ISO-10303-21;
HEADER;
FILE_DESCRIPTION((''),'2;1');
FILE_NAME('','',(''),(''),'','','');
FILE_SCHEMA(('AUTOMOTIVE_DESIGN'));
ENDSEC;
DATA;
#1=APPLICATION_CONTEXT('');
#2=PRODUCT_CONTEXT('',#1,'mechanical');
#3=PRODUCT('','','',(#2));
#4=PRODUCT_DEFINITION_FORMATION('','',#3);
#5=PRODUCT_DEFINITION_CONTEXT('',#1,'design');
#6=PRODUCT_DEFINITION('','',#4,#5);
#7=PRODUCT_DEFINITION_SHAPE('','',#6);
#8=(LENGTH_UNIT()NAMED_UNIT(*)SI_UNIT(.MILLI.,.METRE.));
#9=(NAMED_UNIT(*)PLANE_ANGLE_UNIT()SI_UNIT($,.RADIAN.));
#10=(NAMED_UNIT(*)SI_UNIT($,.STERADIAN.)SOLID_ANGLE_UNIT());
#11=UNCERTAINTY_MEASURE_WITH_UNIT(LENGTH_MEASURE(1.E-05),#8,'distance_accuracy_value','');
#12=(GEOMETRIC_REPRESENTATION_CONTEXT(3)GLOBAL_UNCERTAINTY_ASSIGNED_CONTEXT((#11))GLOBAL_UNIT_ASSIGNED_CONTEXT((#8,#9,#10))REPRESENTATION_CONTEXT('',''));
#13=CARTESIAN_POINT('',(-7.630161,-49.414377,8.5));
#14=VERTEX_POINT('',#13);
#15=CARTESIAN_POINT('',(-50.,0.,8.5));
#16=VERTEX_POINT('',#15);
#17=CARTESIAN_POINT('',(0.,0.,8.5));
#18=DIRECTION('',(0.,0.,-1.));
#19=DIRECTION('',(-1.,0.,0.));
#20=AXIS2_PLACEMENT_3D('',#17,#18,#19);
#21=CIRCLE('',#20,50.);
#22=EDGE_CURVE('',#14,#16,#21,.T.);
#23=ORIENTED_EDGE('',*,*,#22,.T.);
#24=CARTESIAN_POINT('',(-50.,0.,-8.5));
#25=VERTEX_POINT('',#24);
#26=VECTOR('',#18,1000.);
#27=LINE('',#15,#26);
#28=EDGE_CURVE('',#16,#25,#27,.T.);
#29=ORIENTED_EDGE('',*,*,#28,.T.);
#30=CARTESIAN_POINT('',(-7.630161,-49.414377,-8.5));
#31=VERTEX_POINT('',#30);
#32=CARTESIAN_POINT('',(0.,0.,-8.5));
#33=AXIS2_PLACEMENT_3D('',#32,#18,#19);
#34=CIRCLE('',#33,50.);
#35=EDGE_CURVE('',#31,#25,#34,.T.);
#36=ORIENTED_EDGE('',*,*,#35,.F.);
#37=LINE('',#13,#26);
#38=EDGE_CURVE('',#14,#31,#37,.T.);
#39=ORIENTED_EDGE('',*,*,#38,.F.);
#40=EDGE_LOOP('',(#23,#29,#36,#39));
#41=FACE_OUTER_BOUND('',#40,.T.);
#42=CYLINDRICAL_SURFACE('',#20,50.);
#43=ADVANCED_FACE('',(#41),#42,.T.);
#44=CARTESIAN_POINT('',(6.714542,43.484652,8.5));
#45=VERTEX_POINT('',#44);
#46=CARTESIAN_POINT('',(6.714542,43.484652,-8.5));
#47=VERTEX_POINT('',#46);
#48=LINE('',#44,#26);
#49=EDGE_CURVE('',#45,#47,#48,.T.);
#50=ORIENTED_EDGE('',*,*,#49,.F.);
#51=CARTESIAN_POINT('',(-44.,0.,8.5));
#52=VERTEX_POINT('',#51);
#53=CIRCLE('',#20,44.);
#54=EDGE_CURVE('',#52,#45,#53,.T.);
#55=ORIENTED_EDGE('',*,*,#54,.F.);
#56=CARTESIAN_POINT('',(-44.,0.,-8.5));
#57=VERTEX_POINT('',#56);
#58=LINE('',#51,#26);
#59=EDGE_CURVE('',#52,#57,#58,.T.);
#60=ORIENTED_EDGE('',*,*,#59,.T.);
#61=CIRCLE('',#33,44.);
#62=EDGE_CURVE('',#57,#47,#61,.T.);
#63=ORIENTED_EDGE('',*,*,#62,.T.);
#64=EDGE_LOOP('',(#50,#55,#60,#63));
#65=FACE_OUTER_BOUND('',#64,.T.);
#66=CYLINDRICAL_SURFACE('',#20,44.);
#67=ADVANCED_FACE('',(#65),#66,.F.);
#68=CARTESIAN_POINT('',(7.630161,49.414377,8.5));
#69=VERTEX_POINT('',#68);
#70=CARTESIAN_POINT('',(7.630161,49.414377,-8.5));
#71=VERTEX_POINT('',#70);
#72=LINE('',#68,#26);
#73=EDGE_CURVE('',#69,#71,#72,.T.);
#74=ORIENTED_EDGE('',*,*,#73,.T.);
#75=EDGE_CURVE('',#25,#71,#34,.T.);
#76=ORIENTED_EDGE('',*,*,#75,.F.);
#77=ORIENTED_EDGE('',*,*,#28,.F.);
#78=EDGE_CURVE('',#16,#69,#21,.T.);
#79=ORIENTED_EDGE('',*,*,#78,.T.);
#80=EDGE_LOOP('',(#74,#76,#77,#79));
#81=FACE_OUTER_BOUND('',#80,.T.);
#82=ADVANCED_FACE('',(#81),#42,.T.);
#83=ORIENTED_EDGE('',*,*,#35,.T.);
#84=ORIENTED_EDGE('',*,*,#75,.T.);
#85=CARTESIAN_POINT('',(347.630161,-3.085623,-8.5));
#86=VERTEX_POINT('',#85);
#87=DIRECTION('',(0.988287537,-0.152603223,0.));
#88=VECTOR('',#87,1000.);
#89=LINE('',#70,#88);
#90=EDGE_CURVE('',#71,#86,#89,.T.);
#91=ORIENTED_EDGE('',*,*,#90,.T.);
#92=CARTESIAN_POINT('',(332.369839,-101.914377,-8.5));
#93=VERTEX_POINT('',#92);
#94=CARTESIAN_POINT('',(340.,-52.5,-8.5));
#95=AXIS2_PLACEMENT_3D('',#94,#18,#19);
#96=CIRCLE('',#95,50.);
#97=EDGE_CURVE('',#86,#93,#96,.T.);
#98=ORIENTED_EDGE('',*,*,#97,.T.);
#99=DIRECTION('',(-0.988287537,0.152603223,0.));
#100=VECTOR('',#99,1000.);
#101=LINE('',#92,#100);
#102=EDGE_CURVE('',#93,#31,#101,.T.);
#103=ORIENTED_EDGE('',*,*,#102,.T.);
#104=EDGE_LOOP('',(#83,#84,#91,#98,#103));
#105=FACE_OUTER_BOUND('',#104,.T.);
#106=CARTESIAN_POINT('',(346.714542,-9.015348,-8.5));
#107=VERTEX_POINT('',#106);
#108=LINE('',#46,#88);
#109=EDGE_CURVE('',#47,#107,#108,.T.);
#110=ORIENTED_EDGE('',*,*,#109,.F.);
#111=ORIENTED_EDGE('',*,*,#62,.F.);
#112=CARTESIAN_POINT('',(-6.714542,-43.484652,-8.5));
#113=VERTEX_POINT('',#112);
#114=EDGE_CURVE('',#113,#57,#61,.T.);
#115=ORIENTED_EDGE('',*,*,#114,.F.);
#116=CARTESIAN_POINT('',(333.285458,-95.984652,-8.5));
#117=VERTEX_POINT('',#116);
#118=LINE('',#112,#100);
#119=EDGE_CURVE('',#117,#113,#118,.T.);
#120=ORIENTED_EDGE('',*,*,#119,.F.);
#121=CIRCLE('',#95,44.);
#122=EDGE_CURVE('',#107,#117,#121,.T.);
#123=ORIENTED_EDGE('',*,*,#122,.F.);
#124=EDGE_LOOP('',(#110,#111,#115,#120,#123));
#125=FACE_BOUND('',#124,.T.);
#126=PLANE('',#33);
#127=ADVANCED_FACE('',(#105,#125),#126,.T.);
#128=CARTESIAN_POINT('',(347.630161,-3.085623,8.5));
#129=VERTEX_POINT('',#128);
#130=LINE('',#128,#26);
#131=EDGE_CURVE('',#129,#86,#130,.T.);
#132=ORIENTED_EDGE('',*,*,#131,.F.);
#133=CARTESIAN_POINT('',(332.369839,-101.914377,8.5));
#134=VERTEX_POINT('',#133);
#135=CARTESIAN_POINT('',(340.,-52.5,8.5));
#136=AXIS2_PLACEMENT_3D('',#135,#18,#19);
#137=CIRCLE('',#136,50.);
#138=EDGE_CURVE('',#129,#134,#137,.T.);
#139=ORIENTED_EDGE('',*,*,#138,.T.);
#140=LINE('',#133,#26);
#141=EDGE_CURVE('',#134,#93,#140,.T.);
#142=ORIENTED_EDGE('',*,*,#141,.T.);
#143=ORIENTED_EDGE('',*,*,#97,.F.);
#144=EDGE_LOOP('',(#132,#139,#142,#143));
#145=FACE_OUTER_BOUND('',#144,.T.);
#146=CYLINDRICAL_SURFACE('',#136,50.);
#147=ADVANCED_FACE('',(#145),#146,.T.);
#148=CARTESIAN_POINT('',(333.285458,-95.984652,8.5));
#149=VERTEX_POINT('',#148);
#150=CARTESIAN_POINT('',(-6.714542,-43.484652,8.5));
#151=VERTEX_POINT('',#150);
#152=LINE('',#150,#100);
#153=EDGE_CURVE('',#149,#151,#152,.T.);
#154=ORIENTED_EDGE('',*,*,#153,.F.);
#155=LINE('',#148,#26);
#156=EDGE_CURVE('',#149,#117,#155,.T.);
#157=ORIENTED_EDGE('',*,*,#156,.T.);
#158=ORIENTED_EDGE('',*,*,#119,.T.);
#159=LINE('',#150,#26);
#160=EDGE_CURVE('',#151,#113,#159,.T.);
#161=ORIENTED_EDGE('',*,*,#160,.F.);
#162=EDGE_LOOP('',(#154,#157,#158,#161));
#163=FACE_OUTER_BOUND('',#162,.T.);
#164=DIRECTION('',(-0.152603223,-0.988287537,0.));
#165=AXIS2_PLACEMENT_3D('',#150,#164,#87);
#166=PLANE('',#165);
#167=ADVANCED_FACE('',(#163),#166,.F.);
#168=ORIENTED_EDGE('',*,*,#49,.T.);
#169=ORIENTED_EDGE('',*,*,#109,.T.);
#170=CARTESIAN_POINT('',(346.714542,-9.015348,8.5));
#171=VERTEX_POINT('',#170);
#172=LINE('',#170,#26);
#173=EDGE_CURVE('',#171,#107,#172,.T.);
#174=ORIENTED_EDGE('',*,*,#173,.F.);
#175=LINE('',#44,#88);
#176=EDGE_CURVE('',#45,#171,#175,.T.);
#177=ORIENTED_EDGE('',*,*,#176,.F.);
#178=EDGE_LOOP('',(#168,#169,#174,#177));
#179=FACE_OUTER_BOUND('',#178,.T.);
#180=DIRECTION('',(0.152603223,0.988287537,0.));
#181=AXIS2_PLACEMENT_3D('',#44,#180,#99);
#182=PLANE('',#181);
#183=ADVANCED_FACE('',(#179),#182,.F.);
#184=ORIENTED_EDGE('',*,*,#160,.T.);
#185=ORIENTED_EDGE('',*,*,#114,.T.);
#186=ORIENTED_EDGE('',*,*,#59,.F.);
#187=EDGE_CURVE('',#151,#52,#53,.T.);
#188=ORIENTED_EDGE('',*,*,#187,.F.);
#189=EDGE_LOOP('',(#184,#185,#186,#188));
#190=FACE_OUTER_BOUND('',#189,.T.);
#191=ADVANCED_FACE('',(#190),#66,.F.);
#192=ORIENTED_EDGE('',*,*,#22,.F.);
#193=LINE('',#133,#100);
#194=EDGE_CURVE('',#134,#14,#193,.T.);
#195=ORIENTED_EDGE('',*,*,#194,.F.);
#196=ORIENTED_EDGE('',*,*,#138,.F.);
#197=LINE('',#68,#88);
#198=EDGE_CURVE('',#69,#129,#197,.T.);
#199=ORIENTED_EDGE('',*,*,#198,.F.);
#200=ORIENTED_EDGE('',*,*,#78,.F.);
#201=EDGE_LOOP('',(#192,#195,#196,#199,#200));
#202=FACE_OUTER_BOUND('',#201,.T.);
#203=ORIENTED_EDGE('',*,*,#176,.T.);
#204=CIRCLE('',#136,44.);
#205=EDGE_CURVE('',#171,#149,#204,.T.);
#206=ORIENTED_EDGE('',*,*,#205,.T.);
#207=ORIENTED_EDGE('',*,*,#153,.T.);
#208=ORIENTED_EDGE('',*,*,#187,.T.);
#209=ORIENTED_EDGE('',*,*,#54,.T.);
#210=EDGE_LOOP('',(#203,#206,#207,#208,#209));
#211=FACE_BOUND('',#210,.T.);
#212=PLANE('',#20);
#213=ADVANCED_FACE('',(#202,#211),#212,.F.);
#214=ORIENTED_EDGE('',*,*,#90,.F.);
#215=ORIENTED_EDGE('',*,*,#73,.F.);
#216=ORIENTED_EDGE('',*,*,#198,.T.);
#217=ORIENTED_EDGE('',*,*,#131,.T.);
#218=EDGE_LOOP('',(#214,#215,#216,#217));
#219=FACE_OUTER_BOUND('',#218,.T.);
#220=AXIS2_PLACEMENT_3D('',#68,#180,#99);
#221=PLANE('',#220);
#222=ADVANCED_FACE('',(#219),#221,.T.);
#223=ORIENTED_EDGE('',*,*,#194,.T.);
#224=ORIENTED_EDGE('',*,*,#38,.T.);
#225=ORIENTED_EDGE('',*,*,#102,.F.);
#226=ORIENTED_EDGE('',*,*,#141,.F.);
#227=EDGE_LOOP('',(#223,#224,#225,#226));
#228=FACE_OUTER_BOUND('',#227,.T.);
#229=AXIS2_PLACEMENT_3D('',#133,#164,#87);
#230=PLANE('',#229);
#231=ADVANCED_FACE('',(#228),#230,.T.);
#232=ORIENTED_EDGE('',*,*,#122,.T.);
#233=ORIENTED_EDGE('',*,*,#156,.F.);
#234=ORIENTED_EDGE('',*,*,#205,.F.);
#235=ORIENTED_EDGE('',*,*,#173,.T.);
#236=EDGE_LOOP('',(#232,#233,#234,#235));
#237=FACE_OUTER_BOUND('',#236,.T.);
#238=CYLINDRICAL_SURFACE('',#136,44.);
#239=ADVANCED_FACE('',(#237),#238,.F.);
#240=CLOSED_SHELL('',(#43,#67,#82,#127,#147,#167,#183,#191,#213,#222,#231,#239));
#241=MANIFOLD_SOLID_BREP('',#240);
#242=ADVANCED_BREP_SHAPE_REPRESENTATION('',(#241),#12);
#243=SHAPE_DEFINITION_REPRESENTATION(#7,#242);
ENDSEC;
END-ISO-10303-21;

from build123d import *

# Parameters (mm, degrees)
EXTRUDE_THIN1_DEPTH = 8.5


with BuildPart() as part:
    # Sketch2 → Extrude-Thin1 (new, symmetric)
    with BuildSketch(Plane.XY):
        with BuildLine():
            Line((332.369838866, -101.914376866), (-7.630161134, -49.414376866))
            ThreePointArc((-7.630161134, -49.414376866), (-49.414376866, 7.630161134), (7.630161134, 49.414376866))
            Line((7.630161134, 49.414376866), (347.630161134, -3.085623134))
            ThreePointArc((347.630161134, -3.085623134), (389.414376866, -60.130161134), (332.369838866, -101.914376866))
        make_face()
        with BuildLine():
            Line((333.285458202, -95.984651642), (-6.714541798, -43.484651642))
            ThreePointArc((-6.714541798, -43.484651642), (-43.484651642, 6.714541798), (6.714541798, 43.484651642))
            Line((6.714541798, 43.484651642), (346.714541798, -9.015348358))
            ThreePointArc((346.714541798, -9.015348358), (383.484651642, -59.214541798), (333.285458202, -95.984651642))
        make_face(mode=Mode.SUBTRACT)
    extrude(amount=EXTRUDE_THIN1_DEPTH, both=True)


solid = part.part
